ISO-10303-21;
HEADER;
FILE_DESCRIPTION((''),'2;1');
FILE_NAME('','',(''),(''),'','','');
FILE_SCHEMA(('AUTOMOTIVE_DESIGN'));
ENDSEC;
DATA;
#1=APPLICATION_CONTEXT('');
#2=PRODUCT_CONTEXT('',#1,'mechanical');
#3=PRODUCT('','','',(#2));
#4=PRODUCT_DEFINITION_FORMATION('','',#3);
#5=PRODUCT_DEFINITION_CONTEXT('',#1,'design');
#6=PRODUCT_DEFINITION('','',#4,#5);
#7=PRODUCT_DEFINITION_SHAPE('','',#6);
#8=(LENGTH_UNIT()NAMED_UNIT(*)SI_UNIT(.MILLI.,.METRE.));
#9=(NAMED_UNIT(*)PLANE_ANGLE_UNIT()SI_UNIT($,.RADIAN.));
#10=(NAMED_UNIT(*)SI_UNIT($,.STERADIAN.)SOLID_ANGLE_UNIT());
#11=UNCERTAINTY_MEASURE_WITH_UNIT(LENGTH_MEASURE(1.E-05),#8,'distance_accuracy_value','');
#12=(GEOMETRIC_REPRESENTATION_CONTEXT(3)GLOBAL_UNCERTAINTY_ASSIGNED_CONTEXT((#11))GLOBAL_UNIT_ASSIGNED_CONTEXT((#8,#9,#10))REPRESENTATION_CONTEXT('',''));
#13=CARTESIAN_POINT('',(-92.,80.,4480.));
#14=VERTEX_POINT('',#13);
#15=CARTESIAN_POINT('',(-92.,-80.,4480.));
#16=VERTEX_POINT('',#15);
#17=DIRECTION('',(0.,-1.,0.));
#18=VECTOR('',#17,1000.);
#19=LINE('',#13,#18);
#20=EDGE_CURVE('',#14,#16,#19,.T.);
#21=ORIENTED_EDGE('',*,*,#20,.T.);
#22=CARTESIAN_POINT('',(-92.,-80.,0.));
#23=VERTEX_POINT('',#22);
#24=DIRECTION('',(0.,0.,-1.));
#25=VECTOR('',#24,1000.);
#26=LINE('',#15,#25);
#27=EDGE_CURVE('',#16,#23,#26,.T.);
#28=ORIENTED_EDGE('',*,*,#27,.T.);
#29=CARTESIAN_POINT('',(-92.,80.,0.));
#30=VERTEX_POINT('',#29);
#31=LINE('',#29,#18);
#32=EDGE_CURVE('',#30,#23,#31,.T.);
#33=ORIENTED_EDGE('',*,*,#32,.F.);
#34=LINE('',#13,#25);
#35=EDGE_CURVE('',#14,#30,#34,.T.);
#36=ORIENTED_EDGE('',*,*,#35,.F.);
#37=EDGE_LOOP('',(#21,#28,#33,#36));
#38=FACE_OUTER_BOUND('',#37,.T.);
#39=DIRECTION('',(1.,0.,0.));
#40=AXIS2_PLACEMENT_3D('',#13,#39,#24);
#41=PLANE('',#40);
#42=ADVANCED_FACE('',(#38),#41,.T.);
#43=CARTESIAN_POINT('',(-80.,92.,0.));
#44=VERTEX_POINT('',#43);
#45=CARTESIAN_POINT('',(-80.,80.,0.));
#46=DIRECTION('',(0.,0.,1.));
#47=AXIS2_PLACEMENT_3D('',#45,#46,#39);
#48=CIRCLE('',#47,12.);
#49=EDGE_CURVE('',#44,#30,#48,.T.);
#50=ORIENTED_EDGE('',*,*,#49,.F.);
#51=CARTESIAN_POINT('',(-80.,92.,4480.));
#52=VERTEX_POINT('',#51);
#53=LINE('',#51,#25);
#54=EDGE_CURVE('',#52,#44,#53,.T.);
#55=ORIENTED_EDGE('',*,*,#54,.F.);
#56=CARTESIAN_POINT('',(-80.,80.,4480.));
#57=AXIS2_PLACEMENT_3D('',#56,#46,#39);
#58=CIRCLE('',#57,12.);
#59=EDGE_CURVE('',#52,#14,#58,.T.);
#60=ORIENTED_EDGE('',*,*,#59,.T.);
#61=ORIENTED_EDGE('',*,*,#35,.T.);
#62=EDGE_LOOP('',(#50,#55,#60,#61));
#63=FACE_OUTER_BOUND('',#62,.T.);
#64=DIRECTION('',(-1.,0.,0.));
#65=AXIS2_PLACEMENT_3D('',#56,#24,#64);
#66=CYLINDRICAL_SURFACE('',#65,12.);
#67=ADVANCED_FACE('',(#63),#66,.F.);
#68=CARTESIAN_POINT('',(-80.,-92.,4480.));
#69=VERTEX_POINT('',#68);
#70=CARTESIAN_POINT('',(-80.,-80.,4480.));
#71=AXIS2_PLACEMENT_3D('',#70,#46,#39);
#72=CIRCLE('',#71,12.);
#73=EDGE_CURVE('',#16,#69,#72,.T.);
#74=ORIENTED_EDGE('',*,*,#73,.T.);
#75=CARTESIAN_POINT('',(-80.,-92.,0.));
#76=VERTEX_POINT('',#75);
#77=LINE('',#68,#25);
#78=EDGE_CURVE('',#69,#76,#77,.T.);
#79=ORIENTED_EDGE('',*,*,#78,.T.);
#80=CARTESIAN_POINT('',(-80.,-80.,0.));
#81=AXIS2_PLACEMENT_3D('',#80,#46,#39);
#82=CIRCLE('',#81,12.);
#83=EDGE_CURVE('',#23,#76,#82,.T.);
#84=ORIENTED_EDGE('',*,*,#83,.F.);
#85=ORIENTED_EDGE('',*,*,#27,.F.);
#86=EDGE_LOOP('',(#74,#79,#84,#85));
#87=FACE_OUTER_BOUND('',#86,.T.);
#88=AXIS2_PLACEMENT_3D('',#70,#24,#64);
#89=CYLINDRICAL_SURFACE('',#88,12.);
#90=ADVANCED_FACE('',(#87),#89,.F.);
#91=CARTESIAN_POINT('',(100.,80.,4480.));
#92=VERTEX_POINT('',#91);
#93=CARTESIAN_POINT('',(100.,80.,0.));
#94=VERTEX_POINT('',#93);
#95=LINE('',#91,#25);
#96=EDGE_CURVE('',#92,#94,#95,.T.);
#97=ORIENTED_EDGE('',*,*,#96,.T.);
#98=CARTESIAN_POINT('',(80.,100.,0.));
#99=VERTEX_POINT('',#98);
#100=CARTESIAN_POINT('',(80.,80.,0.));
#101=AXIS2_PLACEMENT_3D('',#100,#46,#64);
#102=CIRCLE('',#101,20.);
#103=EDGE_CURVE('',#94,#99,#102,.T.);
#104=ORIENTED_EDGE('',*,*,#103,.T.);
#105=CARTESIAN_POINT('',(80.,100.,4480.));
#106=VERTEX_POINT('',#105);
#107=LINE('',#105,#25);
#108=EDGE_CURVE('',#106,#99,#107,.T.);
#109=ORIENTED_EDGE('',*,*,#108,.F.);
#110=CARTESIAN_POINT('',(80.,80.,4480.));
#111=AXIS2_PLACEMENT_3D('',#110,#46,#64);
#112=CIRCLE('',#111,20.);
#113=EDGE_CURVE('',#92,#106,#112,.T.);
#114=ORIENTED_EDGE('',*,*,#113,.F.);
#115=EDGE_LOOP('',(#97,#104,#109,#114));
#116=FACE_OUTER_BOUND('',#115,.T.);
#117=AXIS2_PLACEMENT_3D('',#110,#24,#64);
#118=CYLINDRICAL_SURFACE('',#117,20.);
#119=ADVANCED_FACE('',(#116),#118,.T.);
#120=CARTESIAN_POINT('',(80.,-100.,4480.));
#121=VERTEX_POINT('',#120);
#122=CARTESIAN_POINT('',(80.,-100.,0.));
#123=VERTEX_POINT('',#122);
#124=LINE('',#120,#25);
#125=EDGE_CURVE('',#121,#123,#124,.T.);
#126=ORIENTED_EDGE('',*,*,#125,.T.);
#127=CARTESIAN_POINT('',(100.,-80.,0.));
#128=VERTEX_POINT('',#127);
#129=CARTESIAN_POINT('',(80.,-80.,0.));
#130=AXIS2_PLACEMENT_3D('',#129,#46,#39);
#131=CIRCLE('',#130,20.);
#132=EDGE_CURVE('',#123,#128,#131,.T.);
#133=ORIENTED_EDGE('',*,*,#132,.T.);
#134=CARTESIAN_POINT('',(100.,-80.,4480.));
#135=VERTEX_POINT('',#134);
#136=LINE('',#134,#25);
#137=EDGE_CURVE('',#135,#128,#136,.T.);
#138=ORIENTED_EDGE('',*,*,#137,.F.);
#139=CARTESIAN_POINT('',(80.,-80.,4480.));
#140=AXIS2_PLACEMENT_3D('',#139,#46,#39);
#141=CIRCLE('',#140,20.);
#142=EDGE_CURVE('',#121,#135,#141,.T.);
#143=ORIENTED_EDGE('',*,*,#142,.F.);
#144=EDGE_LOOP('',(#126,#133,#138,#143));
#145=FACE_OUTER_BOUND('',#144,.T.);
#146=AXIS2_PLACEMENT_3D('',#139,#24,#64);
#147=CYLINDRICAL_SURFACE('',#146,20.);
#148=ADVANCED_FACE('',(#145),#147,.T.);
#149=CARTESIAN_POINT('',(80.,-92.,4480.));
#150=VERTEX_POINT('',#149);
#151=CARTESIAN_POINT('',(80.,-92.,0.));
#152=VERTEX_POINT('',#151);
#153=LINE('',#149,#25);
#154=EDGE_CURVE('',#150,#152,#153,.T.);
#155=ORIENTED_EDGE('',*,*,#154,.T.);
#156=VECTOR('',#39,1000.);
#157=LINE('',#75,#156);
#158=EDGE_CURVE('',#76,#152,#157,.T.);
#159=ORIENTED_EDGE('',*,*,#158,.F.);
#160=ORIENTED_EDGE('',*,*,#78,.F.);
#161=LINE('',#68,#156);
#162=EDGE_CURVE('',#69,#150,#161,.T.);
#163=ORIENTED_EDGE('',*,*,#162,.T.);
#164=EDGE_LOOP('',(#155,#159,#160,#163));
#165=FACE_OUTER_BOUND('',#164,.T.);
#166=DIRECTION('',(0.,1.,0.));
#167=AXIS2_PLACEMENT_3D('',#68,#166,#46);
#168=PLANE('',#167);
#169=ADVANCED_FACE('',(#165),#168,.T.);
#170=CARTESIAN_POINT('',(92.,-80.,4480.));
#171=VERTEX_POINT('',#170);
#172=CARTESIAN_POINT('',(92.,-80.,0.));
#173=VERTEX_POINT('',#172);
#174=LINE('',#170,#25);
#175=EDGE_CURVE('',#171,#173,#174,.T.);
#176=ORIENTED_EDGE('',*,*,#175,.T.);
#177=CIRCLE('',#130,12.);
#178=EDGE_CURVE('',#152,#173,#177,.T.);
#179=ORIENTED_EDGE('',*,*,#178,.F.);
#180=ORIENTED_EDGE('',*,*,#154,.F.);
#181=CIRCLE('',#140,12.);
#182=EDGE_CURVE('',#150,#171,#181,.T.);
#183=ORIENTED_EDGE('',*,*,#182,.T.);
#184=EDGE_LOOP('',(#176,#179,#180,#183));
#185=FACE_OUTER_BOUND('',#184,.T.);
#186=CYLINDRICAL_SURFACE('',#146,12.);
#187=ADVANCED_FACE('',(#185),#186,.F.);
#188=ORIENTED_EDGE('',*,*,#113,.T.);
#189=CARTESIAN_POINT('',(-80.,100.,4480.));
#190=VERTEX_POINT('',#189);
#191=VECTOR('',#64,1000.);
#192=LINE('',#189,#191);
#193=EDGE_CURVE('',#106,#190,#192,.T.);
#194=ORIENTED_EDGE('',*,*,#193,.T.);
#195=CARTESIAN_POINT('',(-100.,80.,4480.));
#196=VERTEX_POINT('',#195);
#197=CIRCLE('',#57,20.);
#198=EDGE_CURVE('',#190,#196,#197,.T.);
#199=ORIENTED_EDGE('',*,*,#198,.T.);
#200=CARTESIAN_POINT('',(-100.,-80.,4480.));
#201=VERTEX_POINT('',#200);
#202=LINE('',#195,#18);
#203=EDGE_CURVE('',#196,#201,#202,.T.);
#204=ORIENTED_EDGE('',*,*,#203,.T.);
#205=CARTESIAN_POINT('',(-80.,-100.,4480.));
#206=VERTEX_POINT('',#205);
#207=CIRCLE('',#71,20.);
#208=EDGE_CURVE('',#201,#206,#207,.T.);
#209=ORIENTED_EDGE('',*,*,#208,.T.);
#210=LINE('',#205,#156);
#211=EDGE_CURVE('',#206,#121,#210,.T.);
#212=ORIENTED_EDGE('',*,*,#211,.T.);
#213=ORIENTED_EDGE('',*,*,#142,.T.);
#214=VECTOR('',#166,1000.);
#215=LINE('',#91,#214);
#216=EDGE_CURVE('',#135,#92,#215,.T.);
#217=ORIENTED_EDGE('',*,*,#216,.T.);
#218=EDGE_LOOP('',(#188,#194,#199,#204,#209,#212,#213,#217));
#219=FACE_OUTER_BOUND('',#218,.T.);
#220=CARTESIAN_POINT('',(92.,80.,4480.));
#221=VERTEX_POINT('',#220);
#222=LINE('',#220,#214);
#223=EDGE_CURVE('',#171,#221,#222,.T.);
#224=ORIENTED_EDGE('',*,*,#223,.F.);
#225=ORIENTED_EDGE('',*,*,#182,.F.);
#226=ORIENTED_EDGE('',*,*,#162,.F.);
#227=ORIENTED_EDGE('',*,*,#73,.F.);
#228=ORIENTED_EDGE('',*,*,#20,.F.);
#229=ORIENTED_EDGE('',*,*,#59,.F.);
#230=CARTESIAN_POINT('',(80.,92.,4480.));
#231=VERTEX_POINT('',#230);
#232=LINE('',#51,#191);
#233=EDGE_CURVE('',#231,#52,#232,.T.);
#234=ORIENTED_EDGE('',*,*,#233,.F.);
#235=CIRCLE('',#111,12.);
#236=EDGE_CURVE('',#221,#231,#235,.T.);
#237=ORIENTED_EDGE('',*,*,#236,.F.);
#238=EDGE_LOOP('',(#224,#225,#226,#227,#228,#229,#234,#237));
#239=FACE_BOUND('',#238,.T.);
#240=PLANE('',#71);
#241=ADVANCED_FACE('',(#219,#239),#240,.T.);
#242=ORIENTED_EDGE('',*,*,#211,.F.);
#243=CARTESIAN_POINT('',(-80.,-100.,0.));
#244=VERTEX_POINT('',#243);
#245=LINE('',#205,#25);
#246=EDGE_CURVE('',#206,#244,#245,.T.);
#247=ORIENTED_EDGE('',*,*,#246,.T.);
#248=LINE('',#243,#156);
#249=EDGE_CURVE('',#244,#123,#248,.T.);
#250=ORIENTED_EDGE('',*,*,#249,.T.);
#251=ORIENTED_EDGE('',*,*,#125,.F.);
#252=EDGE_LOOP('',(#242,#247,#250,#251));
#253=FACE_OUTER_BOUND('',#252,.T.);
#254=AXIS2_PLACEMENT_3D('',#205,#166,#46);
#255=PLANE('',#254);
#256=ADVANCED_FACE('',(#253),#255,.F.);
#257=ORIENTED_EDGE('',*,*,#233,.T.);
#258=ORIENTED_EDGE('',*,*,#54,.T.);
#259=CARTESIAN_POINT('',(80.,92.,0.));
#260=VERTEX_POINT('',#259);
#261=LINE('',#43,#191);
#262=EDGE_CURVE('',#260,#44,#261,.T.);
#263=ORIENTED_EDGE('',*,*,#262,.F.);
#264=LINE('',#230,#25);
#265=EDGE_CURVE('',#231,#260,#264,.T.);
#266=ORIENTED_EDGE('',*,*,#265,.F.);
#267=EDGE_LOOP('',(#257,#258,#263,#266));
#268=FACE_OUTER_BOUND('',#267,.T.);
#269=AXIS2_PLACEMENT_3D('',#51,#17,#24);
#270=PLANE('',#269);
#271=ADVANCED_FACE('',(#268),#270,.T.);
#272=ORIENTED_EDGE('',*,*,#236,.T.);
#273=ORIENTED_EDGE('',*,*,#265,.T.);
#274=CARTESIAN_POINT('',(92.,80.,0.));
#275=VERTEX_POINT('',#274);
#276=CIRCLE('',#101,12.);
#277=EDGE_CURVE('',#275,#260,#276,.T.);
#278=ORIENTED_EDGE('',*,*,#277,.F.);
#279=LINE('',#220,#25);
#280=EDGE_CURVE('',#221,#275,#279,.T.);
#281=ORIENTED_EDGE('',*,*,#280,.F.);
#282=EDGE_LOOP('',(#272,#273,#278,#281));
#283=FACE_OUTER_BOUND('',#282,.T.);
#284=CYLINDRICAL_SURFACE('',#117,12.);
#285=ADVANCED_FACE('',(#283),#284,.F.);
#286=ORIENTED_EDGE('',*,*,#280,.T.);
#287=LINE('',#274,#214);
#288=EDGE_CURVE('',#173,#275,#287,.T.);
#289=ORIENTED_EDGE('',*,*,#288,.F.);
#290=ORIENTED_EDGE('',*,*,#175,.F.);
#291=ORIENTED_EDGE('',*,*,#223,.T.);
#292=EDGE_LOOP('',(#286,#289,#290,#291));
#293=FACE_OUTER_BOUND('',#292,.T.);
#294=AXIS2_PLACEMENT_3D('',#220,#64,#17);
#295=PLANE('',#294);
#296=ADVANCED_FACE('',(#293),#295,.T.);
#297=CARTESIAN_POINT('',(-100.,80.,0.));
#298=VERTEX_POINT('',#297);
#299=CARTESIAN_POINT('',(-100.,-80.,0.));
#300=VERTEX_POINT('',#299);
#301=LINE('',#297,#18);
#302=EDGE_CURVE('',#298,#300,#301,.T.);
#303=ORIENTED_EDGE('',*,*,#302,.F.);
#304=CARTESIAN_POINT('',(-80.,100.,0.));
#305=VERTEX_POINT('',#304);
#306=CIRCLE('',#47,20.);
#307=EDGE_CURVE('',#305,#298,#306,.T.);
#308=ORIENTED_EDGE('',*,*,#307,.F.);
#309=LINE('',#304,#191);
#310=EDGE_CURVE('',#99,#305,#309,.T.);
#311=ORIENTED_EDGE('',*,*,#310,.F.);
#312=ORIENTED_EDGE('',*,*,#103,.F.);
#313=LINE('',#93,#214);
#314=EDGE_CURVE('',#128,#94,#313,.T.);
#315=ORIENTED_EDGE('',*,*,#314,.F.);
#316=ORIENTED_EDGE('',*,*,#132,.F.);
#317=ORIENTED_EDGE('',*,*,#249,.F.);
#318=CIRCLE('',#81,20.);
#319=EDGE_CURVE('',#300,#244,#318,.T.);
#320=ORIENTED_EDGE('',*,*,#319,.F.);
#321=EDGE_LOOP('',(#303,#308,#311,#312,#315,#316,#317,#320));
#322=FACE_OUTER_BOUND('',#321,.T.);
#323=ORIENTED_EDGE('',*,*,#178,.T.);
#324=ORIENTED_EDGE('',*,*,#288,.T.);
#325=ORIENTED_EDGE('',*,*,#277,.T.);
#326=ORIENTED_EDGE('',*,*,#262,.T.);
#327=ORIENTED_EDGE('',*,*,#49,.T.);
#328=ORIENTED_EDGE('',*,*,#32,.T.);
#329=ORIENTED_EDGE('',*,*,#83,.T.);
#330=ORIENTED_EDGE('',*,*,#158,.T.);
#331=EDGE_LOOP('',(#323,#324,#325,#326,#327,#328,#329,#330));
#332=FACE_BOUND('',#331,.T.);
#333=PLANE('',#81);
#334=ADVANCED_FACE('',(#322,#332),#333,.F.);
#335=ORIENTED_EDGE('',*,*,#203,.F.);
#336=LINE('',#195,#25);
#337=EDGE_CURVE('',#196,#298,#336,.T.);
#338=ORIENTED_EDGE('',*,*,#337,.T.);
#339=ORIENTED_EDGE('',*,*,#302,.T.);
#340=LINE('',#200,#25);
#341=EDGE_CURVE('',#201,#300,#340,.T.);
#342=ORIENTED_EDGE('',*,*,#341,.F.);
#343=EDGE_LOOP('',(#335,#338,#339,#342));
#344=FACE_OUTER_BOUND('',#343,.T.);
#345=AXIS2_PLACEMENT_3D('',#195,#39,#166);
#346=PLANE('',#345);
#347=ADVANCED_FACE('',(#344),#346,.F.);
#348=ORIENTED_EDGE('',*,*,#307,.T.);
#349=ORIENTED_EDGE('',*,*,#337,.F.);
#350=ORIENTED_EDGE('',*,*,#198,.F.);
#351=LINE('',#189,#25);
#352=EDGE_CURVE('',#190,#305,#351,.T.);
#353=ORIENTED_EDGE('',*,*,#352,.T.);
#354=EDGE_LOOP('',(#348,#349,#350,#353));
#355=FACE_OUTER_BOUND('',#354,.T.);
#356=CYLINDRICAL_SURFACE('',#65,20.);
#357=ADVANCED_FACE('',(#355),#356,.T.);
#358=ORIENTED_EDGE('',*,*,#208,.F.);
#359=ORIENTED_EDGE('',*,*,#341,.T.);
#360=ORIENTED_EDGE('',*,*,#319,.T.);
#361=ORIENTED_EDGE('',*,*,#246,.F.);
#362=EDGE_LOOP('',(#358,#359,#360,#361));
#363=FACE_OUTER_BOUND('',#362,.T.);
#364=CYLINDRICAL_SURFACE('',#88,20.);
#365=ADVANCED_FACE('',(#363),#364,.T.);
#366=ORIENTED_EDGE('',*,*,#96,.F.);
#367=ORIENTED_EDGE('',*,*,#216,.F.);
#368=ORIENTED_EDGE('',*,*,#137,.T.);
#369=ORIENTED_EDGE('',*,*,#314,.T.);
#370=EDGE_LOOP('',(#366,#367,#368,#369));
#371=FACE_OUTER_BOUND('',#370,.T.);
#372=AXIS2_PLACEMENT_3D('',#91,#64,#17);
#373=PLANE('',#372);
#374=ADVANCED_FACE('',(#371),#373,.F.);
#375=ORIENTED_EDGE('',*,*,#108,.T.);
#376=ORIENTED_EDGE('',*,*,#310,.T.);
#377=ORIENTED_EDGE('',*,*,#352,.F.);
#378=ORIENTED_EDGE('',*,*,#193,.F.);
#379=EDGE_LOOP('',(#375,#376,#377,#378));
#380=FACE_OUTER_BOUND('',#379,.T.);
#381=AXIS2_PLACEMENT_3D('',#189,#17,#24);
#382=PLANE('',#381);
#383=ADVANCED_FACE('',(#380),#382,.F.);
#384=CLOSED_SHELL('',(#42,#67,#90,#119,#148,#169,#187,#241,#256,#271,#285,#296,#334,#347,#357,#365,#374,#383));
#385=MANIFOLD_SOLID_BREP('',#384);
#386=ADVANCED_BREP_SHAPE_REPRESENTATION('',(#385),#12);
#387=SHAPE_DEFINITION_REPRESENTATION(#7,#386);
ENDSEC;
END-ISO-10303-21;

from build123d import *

# Parameters (mm, degrees)
BOSS_EXTRUDE1_DEPTH = 4480


with BuildPart() as part:
    # Sketch1 → Boss-Extrude1 (new body)
    with BuildSketch(Plane.XY):
        with BuildLine():
            Line((-80, 100), (80, 100))
            ThreePointArc((80, 100), (94.142135624, 94.142135624), (100, 80))
            Line((100, 80), (100, -80))
            ThreePointArc((100, -80), (94.142135624, -94.142135624), (80, -100))
            Line((80, -100), (-80, -100))
            ThreePointArc((-80, -100), (-94.142135624, -94.142135624), (-100, -80))
            Line((-100, -80), (-100, 80))
            ThreePointArc((-100, 80), (-94.142135624, 94.142135624), (-80, 100))
        make_face()
        with BuildLine():
            Line((-92, 80), (-92, -80))
            ThreePointArc((-92, -80), (-88.485281374, -88.485281374), (-80, -92))
            Line((-80, -92), (80, -92))
            ThreePointArc((80, -92), (88.485281374, -88.485281374), (92, -80))
            Line((92, -80), (92, 80))
            ThreePointArc((92, 80), (88.485281374, 88.485281374), (80, 92))
            Line((80, 92), (-80, 92))
            ThreePointArc((-80, 92), (-88.485281374, 88.485281374), (-92, 80))
        make_face(mode=Mode.SUBTRACT)
    extrude(amount=BOSS_EXTRUDE1_DEPTH)


solid = part.part
